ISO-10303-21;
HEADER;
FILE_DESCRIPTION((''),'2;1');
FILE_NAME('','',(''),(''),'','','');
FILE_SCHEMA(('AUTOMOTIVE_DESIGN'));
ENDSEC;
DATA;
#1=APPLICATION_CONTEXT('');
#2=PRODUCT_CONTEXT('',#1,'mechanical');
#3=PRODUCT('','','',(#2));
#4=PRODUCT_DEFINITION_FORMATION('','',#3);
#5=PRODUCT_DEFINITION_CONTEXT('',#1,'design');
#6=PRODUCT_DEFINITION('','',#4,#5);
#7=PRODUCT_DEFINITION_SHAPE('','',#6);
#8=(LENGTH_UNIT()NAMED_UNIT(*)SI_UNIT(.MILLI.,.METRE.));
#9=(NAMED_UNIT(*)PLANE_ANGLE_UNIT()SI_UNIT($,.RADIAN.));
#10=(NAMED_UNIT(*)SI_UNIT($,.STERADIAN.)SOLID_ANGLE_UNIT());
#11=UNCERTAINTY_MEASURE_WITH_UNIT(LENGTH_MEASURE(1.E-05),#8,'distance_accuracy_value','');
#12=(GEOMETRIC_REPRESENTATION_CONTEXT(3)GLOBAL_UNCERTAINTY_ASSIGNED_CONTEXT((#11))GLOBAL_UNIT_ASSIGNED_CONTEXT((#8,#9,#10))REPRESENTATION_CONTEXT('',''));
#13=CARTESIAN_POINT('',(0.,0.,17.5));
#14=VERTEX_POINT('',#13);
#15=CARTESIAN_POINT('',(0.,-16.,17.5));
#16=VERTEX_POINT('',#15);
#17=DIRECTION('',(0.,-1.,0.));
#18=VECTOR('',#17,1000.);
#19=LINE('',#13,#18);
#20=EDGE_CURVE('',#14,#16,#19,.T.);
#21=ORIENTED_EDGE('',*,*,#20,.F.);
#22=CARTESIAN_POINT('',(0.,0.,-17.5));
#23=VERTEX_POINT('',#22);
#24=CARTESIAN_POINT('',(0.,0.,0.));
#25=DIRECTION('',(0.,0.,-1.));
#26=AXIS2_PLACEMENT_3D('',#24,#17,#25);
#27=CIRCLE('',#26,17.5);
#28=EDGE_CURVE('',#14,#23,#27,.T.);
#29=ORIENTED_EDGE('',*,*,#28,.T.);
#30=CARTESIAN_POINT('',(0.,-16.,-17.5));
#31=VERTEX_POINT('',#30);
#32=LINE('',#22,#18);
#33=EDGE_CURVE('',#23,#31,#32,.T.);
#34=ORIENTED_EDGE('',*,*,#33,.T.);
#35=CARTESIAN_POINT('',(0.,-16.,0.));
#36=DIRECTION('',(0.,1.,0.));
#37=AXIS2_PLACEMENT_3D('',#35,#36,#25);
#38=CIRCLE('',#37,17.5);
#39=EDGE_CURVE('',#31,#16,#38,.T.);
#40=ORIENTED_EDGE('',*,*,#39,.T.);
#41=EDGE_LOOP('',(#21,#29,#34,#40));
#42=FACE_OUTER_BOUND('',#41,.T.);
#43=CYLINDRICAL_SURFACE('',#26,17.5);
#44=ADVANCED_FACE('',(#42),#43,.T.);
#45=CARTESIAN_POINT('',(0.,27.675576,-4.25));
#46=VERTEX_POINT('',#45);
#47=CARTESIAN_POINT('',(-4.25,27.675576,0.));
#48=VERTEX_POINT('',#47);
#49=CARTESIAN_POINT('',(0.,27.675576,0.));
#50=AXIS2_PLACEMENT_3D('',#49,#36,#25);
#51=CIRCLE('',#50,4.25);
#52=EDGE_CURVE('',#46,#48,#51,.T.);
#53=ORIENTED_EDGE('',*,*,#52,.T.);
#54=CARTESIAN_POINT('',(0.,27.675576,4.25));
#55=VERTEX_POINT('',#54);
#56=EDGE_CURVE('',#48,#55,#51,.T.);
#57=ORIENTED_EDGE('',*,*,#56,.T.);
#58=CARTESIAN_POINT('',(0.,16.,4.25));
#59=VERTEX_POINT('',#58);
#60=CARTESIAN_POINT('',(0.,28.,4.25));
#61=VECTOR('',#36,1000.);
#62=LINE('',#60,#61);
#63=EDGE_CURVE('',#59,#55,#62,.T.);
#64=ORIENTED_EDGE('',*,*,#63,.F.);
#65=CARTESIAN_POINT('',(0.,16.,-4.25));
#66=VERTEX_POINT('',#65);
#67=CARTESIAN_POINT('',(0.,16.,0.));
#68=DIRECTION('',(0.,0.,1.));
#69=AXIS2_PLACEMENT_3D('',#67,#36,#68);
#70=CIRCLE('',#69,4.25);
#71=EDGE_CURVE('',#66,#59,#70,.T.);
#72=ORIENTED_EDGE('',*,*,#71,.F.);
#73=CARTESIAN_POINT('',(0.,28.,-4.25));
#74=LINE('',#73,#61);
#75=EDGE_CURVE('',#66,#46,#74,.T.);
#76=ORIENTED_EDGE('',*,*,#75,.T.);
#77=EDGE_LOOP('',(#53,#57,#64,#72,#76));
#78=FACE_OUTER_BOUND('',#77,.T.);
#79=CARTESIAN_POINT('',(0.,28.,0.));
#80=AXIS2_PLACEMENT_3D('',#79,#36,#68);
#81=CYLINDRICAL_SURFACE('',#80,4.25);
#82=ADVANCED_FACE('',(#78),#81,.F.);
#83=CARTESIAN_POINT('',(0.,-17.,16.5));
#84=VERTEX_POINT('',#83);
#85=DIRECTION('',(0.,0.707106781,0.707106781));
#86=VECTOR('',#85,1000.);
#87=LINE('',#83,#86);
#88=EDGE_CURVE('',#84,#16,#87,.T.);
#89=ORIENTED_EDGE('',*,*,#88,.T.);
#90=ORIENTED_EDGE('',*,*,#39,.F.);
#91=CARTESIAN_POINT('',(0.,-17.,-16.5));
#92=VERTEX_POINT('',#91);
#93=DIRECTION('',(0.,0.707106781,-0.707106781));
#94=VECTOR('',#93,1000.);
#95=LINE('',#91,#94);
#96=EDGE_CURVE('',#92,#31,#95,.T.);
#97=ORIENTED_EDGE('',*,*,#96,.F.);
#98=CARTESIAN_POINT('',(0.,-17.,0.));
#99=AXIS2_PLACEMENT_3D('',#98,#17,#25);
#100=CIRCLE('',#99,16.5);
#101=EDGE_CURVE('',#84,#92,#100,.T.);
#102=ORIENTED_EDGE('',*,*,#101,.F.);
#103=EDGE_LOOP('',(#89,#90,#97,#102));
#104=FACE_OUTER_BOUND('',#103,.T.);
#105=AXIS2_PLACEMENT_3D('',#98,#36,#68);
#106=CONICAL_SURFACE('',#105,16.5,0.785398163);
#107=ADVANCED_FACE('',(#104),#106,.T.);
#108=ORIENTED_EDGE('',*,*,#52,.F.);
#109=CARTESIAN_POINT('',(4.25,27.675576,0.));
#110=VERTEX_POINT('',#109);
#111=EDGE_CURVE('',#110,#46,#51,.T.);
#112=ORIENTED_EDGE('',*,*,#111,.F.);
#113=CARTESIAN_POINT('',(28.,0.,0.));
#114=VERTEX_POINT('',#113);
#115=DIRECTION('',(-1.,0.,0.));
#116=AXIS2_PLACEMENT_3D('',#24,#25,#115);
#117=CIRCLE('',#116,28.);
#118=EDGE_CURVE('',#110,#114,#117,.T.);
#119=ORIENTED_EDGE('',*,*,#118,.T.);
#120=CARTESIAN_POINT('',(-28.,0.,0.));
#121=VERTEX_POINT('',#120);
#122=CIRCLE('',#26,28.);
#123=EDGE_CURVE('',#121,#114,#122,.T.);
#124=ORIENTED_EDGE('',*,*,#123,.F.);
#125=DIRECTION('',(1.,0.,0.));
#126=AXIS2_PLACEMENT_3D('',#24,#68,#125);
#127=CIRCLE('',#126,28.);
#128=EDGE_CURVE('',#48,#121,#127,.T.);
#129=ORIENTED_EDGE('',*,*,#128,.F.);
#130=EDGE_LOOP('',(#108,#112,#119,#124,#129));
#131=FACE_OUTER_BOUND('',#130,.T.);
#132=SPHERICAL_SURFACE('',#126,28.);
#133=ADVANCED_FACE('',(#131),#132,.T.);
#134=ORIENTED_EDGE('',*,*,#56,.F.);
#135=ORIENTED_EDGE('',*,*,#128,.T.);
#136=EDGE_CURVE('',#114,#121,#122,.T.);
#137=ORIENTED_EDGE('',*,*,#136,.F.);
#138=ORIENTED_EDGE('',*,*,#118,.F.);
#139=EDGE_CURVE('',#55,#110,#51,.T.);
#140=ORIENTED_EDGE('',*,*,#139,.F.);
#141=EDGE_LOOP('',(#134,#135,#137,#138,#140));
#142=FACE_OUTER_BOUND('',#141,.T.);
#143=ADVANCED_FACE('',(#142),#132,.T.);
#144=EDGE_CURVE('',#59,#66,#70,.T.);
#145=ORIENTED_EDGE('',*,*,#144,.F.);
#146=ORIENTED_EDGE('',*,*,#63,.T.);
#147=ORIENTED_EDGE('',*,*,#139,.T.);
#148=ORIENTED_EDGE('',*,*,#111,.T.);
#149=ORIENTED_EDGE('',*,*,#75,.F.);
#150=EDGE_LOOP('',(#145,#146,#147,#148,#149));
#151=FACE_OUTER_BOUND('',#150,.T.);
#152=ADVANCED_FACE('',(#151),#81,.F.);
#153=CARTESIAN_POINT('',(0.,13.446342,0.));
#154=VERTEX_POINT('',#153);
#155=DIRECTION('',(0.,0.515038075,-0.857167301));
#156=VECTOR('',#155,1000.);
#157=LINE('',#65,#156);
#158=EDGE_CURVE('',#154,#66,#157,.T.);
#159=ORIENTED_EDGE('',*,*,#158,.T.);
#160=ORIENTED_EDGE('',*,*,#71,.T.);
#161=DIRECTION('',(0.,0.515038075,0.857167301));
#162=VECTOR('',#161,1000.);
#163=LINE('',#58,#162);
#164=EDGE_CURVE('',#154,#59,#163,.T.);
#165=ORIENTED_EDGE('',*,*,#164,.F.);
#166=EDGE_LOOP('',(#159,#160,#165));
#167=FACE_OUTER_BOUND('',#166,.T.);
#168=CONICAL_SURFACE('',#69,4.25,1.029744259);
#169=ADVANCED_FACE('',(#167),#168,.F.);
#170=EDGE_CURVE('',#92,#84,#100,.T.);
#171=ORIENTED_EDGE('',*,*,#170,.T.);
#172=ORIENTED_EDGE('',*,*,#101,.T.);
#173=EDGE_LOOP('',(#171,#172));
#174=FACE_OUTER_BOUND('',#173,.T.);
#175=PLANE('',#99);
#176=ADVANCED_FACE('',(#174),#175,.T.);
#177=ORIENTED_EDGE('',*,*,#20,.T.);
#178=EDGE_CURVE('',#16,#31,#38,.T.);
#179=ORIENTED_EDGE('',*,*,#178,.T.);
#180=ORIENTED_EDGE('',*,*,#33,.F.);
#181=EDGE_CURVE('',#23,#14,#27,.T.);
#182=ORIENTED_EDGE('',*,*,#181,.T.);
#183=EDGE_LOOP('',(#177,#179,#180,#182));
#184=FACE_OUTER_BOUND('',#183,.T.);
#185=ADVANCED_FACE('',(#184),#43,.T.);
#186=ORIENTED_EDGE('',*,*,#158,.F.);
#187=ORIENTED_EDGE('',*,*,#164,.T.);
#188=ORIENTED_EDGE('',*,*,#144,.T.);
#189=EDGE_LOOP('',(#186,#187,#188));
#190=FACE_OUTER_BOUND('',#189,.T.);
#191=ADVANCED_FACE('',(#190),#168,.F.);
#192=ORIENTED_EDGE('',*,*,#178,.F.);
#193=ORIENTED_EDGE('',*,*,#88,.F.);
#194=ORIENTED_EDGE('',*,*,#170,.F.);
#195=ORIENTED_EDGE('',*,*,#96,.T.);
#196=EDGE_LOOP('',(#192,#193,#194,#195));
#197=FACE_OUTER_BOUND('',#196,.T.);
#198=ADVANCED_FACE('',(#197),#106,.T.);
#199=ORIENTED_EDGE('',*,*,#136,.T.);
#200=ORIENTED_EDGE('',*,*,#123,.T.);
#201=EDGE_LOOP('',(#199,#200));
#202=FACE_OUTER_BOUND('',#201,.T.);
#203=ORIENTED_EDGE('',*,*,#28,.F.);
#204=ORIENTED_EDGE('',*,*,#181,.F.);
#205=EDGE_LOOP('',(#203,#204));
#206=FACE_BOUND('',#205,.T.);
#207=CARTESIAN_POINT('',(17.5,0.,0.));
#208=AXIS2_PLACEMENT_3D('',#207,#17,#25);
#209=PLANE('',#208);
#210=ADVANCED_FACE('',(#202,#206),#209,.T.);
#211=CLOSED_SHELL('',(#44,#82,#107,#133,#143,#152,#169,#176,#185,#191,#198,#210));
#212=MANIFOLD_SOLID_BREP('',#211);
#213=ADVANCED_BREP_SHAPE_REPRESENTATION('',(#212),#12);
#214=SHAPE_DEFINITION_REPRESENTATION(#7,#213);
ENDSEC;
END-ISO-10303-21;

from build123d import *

# Parameters (mm, degrees)
HOLE_WIZARD_M10_1_D     = 8.5
HOLE_WIZARD_M10_1_DEPTH = 12
HOLE_WIZARD_M10_1_TIP   = 2.553657631
CHAMFER_1_SIZE          = 1


with BuildPart() as part:
    # 草图1 → 旋转1 (revolve)
    with BuildSketch(Plane.XY, mode=Mode.PRIVATE) as revolve_1_sk:
        with BuildLine():
            Line((17.5, 0), (28, 0))
            ThreePointArc((28, 0), (19.798989873, 19.798989873), (0, 28))
            Line((0, 28), (0, 0))
            Line((0, 0), (0, -17))
            Line((0, -17), (17.5, -17))
            Line((17.5, -17), (17.5, 0))
        make_face()
    revolve(revolve_1_sk.sketch.rotate(Axis((0, 0, 0), (0, 1, 0)), 90), axis=Axis((0, 0, 0), (0, 1, 0)))

    # M10 螺纹孔1
    with Locations(Plane(origin=(0, 28, 0), x_dir=(1, 0, 0), z_dir=(0, 1, 0))):
        with Locations((0, 0)):
            Hole(HOLE_WIZARD_M10_1_D / 2, depth=HOLE_WIZARD_M10_1_DEPTH)
            with Locations((0, 0, -(HOLE_WIZARD_M10_1_DEPTH + HOLE_WIZARD_M10_1_TIP / 2))):  # 118° drill point
                Cone(0, HOLE_WIZARD_M10_1_D / 2, HOLE_WIZARD_M10_1_TIP, mode=Mode.SUBTRACT)

    # 倒角1
    chamfer_1_edges = [part.edges().sort_by_distance(p)[0] for p in [
        (0, -17, 17.5),
    ]]
    chamfer(chamfer_1_edges, length=CHAMFER_1_SIZE)


solid = part.part
